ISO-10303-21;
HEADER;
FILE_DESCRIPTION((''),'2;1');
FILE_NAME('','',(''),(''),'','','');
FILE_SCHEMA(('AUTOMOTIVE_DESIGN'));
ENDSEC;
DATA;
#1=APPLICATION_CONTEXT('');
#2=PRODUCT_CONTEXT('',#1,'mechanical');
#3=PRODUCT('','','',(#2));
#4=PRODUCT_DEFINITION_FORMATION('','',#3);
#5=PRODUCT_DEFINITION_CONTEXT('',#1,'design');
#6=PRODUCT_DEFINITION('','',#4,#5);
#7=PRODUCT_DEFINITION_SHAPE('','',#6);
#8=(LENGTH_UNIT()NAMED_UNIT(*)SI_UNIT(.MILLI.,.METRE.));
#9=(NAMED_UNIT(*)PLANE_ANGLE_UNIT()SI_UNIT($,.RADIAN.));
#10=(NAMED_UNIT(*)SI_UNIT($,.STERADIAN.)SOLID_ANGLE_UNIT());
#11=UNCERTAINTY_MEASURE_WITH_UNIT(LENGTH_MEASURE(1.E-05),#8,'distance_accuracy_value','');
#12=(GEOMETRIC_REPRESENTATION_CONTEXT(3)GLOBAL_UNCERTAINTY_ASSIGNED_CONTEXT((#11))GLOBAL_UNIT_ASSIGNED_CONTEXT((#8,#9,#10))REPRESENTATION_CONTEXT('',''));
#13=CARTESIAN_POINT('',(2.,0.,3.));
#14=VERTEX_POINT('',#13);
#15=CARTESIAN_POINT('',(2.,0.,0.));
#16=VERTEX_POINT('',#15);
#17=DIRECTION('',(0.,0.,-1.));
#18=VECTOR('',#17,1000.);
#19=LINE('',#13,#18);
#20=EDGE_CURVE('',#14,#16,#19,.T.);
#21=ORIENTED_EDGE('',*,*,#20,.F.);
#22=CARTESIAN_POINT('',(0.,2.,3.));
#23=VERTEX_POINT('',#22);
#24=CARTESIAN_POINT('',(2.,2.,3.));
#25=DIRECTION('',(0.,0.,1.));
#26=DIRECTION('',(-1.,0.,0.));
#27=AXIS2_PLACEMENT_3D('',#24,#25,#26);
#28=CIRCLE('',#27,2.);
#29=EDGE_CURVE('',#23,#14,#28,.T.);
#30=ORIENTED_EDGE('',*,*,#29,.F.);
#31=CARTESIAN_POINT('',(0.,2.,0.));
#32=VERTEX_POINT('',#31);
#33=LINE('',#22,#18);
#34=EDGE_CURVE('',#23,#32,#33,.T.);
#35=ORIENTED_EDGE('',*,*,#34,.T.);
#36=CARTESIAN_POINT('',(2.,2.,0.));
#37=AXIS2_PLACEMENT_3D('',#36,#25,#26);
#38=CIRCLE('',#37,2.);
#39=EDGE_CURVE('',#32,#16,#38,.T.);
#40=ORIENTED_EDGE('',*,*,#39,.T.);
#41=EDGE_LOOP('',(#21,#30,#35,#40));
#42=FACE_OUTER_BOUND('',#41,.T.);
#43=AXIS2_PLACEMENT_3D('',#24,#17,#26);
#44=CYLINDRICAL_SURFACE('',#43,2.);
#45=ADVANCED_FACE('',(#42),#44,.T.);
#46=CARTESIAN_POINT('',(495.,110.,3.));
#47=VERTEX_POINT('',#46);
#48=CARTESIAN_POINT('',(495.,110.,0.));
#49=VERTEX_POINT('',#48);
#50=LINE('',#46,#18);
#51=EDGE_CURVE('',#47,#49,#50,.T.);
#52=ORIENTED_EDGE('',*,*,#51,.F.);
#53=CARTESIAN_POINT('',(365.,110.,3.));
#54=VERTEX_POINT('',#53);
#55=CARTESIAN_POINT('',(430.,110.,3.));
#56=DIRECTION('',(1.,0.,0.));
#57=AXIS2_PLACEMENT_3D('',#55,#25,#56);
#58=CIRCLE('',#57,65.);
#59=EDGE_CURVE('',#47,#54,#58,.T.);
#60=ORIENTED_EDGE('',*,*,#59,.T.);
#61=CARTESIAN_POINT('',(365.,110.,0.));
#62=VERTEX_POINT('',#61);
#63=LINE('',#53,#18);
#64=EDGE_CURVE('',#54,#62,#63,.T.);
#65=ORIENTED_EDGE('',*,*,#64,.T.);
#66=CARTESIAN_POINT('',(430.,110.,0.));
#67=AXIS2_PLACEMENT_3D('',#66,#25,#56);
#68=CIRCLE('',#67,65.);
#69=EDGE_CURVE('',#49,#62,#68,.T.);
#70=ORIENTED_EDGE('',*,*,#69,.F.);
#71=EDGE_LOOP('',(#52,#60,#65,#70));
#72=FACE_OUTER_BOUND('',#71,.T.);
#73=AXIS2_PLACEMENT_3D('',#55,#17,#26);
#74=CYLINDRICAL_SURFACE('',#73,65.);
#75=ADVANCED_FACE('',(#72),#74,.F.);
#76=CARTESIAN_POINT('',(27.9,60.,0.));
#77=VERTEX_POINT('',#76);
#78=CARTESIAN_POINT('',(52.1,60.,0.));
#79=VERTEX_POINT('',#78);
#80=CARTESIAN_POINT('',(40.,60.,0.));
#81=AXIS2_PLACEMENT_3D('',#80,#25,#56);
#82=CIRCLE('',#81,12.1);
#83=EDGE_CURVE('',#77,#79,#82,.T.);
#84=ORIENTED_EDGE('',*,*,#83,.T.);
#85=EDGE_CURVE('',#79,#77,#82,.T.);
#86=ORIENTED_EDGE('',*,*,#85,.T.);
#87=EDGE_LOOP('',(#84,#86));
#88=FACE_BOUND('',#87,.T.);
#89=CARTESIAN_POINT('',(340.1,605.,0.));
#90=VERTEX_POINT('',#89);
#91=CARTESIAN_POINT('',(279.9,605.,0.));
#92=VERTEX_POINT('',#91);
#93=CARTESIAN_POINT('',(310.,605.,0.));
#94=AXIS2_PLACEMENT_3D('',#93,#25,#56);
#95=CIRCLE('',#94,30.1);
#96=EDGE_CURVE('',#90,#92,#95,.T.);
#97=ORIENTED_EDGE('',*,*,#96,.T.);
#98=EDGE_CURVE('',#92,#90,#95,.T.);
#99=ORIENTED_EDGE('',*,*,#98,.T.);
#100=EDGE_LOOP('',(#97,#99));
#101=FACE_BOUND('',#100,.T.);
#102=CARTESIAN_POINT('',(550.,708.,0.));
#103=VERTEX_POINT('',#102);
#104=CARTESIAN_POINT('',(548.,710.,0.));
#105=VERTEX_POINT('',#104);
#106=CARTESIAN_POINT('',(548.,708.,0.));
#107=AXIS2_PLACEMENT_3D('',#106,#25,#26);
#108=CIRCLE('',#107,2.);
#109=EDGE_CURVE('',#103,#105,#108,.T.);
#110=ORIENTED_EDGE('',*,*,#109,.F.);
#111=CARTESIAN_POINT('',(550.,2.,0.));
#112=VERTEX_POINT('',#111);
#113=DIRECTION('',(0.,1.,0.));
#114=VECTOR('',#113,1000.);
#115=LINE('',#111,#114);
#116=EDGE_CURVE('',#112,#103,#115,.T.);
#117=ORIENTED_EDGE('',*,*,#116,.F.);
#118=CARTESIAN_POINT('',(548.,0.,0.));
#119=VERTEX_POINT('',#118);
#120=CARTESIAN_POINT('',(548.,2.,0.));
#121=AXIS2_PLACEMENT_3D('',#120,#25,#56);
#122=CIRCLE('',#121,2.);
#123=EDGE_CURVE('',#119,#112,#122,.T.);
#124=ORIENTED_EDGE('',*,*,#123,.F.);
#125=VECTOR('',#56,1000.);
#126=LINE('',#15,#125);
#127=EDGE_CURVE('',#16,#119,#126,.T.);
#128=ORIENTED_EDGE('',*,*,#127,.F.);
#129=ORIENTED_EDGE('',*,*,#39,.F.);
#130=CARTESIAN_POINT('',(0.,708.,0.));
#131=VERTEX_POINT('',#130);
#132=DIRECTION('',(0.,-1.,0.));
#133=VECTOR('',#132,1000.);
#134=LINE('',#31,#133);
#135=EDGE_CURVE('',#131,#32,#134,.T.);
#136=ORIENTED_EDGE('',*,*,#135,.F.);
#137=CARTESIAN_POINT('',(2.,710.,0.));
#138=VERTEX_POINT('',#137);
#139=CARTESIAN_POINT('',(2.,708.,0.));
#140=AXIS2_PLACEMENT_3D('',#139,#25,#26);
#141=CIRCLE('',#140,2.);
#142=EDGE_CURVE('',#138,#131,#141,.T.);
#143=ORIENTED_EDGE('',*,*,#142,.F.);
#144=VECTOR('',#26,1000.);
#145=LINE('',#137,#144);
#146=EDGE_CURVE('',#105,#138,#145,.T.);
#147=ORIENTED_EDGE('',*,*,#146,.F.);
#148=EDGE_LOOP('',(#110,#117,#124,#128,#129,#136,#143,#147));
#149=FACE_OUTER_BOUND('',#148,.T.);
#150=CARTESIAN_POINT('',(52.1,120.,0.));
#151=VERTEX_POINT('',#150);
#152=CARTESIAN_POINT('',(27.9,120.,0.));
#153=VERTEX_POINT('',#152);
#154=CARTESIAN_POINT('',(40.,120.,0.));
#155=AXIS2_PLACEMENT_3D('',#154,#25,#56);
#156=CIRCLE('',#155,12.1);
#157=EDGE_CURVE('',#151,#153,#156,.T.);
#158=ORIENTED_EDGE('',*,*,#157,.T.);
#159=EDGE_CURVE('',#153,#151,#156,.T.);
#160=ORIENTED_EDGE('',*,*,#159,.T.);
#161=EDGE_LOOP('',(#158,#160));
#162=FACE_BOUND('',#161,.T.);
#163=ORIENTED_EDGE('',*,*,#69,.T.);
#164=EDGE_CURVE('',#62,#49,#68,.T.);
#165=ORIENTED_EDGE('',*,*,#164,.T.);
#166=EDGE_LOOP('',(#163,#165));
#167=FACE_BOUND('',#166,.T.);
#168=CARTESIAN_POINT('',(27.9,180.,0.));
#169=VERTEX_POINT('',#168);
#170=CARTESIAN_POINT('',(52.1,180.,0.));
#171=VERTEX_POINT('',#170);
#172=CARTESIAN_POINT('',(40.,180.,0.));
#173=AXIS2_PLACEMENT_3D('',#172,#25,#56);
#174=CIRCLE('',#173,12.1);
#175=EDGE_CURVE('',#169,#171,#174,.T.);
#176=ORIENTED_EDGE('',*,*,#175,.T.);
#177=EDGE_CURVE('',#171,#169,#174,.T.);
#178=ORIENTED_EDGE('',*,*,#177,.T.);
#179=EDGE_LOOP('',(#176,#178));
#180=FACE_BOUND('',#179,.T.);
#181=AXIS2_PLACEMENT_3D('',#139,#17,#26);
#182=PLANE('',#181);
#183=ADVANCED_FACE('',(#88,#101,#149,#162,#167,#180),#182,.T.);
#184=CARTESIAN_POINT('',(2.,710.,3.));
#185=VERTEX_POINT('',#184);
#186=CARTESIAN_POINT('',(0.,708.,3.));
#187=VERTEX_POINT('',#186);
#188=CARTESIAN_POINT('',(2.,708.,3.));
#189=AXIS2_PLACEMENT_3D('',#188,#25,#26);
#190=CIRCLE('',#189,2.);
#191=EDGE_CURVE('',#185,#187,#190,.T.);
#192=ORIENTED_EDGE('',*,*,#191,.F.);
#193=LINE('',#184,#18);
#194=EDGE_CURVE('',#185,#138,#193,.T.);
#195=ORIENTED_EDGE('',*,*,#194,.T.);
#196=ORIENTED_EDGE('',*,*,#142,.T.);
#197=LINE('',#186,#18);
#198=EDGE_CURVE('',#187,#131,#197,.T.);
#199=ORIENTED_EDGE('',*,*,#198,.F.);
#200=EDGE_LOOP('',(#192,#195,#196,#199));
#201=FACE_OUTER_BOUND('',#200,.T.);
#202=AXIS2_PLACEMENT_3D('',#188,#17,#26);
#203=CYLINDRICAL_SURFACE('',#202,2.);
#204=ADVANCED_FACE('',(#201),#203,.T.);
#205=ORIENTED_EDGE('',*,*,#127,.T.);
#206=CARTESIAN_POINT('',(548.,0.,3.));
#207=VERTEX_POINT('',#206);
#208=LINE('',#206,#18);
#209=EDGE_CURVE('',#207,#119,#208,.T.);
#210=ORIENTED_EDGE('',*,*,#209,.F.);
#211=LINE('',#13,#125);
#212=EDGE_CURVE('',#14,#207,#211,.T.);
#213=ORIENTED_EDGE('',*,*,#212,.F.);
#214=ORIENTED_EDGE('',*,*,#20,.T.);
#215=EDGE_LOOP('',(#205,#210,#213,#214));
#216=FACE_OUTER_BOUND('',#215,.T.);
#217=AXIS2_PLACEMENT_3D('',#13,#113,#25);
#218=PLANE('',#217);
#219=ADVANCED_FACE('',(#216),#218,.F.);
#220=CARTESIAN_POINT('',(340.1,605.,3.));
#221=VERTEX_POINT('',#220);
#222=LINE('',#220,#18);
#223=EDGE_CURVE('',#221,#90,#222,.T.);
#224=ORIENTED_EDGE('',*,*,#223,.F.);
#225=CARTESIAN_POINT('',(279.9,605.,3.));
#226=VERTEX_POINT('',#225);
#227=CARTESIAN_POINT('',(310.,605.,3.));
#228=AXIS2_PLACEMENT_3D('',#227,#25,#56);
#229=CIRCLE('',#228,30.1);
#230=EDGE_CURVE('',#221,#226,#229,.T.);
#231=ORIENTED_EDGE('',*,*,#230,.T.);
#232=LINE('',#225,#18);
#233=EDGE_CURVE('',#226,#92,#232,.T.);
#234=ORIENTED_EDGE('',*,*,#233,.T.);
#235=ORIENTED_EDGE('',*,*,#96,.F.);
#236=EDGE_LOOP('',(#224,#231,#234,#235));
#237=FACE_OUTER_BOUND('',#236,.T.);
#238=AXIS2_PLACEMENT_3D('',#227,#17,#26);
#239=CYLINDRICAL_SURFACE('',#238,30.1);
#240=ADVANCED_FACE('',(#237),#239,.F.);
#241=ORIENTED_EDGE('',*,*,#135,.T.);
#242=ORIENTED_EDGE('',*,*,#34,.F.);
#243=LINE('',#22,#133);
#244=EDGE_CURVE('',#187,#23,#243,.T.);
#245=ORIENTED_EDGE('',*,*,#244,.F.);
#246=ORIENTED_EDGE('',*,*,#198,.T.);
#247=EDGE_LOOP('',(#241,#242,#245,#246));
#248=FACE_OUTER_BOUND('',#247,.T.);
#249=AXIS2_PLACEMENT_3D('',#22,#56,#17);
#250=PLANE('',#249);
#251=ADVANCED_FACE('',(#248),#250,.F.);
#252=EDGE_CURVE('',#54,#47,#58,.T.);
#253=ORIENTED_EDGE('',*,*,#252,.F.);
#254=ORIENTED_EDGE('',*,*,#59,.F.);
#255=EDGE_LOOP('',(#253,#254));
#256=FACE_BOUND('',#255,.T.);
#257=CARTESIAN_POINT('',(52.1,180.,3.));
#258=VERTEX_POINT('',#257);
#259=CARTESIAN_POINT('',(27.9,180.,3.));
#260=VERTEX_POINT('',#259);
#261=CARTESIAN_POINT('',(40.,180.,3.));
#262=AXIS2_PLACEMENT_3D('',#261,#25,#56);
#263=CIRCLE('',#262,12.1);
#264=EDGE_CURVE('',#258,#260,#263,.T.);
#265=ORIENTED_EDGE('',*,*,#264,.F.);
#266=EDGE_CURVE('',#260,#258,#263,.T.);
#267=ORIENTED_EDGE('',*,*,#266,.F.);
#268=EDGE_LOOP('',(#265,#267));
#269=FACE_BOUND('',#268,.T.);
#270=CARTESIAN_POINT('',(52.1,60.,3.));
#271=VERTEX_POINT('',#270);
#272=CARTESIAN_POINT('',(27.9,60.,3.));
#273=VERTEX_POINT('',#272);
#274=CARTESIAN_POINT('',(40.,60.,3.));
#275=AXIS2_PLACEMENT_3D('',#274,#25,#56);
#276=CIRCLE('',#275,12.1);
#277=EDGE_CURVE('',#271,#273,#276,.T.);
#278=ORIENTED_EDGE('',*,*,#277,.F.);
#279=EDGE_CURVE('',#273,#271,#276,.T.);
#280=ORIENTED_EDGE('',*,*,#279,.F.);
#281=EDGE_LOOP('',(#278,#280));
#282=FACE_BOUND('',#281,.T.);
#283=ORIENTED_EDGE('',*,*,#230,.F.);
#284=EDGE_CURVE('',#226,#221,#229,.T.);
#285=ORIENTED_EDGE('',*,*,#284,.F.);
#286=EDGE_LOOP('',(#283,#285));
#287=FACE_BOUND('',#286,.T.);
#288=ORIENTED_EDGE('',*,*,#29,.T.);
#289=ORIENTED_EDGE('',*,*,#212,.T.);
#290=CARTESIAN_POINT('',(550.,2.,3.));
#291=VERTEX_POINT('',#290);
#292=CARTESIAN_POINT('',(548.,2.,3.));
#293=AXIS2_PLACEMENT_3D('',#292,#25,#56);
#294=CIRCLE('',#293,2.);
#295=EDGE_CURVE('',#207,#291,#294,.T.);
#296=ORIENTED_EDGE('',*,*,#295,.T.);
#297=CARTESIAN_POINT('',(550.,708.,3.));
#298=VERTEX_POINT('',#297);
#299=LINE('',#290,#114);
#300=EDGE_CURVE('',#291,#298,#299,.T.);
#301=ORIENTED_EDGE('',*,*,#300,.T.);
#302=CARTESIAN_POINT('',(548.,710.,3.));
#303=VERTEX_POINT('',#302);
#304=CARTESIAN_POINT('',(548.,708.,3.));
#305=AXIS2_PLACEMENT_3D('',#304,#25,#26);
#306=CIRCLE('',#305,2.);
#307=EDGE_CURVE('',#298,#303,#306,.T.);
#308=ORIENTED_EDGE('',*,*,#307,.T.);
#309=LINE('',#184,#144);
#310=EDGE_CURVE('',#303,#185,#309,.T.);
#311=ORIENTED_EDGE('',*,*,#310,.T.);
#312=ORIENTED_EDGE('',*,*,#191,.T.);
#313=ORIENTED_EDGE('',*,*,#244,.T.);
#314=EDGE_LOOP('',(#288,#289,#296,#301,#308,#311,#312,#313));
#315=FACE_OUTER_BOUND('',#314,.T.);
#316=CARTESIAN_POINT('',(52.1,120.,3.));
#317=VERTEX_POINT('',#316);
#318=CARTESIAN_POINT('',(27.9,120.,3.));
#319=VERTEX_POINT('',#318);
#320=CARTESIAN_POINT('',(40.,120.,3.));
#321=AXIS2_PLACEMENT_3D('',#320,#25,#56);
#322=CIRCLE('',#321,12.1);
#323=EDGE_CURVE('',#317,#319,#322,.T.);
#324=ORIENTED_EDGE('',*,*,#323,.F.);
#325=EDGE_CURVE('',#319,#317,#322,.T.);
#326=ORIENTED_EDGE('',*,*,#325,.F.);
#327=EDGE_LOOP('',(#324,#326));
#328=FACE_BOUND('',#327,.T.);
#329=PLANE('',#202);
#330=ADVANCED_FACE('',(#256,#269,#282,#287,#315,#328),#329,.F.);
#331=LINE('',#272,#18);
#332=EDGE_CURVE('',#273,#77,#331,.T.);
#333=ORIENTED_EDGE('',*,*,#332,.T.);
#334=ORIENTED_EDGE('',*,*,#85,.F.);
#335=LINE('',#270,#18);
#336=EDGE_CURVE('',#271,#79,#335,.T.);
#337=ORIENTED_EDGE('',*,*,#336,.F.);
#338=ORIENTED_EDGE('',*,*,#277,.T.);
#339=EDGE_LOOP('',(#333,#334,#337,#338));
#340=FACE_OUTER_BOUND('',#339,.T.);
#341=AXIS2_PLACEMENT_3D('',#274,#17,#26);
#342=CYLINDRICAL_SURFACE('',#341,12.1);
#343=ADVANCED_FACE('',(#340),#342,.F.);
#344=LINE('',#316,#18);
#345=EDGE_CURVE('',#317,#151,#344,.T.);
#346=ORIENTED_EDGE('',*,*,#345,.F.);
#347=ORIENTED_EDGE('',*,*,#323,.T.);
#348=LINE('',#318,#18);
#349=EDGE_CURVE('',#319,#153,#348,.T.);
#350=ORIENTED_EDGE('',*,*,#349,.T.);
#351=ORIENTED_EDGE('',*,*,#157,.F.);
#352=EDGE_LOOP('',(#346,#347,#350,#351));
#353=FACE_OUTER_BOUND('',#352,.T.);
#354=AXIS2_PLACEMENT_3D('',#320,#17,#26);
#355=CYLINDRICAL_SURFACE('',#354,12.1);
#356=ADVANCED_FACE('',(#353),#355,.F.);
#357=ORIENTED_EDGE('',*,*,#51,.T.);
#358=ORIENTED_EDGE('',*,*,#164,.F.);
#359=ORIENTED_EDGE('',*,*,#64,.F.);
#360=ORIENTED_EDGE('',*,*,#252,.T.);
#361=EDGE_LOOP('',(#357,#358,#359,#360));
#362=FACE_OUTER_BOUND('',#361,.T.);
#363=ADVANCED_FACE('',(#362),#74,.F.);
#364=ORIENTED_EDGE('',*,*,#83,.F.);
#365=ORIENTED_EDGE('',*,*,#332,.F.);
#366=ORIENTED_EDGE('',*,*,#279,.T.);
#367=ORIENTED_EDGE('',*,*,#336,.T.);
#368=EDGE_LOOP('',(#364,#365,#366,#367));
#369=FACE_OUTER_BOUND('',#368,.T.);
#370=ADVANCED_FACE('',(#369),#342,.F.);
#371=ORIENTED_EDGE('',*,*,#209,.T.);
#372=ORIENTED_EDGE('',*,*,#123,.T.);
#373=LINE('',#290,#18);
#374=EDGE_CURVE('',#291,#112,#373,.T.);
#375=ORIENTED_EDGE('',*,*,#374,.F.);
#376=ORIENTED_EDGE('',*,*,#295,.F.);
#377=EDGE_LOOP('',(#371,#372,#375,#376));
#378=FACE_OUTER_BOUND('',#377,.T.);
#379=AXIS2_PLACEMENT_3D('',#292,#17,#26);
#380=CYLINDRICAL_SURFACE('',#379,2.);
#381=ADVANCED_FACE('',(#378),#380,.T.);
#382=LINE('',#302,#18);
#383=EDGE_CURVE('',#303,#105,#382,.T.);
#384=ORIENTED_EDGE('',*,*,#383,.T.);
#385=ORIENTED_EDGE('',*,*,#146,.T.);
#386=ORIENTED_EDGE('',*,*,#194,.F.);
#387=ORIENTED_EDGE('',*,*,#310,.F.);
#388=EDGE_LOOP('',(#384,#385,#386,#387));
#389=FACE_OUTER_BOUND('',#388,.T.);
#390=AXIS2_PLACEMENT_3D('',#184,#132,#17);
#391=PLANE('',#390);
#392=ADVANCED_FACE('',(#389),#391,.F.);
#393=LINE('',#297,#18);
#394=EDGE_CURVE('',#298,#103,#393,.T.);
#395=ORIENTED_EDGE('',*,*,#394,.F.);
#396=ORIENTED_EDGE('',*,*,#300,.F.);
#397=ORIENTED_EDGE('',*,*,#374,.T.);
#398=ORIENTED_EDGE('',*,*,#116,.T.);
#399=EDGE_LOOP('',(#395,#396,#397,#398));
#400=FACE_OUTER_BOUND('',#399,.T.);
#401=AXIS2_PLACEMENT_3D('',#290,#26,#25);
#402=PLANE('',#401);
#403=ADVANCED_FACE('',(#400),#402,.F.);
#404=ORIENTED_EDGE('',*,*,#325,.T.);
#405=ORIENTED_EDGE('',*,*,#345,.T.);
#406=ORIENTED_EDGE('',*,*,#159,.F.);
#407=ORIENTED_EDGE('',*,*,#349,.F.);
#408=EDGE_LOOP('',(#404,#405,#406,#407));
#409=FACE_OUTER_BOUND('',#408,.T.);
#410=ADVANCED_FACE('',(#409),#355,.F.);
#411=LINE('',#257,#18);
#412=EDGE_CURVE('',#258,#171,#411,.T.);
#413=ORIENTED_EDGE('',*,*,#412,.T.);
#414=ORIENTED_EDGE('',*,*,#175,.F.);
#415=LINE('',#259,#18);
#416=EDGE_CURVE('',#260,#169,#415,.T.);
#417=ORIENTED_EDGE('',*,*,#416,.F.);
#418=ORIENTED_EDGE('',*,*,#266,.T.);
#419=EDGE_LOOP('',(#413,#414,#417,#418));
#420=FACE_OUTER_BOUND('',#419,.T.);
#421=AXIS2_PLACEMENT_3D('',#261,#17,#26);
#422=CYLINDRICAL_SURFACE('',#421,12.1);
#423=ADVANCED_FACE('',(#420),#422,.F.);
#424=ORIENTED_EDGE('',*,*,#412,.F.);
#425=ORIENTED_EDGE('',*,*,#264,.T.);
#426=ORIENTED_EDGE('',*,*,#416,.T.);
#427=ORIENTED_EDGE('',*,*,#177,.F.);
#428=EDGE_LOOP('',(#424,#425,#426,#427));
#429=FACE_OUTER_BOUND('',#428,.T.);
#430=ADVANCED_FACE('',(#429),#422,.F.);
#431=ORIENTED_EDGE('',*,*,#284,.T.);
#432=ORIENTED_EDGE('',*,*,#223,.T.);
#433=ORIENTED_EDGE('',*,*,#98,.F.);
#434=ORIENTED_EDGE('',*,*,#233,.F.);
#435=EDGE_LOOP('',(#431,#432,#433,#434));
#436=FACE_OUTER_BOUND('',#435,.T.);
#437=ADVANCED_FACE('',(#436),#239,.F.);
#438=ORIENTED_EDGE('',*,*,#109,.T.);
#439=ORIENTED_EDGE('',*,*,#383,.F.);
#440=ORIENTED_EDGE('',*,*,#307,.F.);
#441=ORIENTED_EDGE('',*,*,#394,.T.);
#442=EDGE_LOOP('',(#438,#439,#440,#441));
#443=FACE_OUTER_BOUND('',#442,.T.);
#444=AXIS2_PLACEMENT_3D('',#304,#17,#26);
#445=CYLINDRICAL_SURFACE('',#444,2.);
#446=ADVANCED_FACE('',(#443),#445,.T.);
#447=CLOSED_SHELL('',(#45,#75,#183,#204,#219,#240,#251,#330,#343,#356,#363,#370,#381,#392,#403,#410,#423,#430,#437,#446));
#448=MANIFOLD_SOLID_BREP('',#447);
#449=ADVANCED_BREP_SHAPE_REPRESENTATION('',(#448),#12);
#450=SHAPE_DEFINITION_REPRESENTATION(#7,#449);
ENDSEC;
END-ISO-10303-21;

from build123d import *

# Parameters (mm, degrees)
SKETCH1_R           = 12.1
SKETCH1_R_2         = 65
SKETCH1_R_3         = 30.1
BOSS_EXTRUDE1_DEPTH = 3


with BuildPart() as part:
    # Sketch1 → Boss-Extrude1 (new body)
    with BuildSketch(Plane.XY):
        with BuildLine():
            Line((2, 0), (548, 0))
            ThreePointArc((548, 0), (549.414213562, 0.585786438), (550, 2))
            Line((550, 2), (550, 708))
            ThreePointArc((550, 708), (549.414213562, 709.414213562), (548, 710))
            Line((548, 710), (2, 710))
            ThreePointArc((2, 710), (0.585786438, 709.414213562), (0, 708))
            Line((0, 708), (0, 2))
            ThreePointArc((0, 2), (0.585786438, 0.585786438), (2, 0))
        make_face()
        with Locations((40, 60)):
            Circle(SKETCH1_R, mode=Mode.SUBTRACT)
        with Locations((40, 120)):
            Circle(SKETCH1_R, mode=Mode.SUBTRACT)
        with Locations((40, 180)):
            Circle(SKETCH1_R, mode=Mode.SUBTRACT)
        with Locations((430, 110)):
            Circle(SKETCH1_R_2, mode=Mode.SUBTRACT)
        with Locations((310, 605)):
            Circle(SKETCH1_R_3, mode=Mode.SUBTRACT)
    extrude(amount=BOSS_EXTRUDE1_DEPTH)


solid = part.part
